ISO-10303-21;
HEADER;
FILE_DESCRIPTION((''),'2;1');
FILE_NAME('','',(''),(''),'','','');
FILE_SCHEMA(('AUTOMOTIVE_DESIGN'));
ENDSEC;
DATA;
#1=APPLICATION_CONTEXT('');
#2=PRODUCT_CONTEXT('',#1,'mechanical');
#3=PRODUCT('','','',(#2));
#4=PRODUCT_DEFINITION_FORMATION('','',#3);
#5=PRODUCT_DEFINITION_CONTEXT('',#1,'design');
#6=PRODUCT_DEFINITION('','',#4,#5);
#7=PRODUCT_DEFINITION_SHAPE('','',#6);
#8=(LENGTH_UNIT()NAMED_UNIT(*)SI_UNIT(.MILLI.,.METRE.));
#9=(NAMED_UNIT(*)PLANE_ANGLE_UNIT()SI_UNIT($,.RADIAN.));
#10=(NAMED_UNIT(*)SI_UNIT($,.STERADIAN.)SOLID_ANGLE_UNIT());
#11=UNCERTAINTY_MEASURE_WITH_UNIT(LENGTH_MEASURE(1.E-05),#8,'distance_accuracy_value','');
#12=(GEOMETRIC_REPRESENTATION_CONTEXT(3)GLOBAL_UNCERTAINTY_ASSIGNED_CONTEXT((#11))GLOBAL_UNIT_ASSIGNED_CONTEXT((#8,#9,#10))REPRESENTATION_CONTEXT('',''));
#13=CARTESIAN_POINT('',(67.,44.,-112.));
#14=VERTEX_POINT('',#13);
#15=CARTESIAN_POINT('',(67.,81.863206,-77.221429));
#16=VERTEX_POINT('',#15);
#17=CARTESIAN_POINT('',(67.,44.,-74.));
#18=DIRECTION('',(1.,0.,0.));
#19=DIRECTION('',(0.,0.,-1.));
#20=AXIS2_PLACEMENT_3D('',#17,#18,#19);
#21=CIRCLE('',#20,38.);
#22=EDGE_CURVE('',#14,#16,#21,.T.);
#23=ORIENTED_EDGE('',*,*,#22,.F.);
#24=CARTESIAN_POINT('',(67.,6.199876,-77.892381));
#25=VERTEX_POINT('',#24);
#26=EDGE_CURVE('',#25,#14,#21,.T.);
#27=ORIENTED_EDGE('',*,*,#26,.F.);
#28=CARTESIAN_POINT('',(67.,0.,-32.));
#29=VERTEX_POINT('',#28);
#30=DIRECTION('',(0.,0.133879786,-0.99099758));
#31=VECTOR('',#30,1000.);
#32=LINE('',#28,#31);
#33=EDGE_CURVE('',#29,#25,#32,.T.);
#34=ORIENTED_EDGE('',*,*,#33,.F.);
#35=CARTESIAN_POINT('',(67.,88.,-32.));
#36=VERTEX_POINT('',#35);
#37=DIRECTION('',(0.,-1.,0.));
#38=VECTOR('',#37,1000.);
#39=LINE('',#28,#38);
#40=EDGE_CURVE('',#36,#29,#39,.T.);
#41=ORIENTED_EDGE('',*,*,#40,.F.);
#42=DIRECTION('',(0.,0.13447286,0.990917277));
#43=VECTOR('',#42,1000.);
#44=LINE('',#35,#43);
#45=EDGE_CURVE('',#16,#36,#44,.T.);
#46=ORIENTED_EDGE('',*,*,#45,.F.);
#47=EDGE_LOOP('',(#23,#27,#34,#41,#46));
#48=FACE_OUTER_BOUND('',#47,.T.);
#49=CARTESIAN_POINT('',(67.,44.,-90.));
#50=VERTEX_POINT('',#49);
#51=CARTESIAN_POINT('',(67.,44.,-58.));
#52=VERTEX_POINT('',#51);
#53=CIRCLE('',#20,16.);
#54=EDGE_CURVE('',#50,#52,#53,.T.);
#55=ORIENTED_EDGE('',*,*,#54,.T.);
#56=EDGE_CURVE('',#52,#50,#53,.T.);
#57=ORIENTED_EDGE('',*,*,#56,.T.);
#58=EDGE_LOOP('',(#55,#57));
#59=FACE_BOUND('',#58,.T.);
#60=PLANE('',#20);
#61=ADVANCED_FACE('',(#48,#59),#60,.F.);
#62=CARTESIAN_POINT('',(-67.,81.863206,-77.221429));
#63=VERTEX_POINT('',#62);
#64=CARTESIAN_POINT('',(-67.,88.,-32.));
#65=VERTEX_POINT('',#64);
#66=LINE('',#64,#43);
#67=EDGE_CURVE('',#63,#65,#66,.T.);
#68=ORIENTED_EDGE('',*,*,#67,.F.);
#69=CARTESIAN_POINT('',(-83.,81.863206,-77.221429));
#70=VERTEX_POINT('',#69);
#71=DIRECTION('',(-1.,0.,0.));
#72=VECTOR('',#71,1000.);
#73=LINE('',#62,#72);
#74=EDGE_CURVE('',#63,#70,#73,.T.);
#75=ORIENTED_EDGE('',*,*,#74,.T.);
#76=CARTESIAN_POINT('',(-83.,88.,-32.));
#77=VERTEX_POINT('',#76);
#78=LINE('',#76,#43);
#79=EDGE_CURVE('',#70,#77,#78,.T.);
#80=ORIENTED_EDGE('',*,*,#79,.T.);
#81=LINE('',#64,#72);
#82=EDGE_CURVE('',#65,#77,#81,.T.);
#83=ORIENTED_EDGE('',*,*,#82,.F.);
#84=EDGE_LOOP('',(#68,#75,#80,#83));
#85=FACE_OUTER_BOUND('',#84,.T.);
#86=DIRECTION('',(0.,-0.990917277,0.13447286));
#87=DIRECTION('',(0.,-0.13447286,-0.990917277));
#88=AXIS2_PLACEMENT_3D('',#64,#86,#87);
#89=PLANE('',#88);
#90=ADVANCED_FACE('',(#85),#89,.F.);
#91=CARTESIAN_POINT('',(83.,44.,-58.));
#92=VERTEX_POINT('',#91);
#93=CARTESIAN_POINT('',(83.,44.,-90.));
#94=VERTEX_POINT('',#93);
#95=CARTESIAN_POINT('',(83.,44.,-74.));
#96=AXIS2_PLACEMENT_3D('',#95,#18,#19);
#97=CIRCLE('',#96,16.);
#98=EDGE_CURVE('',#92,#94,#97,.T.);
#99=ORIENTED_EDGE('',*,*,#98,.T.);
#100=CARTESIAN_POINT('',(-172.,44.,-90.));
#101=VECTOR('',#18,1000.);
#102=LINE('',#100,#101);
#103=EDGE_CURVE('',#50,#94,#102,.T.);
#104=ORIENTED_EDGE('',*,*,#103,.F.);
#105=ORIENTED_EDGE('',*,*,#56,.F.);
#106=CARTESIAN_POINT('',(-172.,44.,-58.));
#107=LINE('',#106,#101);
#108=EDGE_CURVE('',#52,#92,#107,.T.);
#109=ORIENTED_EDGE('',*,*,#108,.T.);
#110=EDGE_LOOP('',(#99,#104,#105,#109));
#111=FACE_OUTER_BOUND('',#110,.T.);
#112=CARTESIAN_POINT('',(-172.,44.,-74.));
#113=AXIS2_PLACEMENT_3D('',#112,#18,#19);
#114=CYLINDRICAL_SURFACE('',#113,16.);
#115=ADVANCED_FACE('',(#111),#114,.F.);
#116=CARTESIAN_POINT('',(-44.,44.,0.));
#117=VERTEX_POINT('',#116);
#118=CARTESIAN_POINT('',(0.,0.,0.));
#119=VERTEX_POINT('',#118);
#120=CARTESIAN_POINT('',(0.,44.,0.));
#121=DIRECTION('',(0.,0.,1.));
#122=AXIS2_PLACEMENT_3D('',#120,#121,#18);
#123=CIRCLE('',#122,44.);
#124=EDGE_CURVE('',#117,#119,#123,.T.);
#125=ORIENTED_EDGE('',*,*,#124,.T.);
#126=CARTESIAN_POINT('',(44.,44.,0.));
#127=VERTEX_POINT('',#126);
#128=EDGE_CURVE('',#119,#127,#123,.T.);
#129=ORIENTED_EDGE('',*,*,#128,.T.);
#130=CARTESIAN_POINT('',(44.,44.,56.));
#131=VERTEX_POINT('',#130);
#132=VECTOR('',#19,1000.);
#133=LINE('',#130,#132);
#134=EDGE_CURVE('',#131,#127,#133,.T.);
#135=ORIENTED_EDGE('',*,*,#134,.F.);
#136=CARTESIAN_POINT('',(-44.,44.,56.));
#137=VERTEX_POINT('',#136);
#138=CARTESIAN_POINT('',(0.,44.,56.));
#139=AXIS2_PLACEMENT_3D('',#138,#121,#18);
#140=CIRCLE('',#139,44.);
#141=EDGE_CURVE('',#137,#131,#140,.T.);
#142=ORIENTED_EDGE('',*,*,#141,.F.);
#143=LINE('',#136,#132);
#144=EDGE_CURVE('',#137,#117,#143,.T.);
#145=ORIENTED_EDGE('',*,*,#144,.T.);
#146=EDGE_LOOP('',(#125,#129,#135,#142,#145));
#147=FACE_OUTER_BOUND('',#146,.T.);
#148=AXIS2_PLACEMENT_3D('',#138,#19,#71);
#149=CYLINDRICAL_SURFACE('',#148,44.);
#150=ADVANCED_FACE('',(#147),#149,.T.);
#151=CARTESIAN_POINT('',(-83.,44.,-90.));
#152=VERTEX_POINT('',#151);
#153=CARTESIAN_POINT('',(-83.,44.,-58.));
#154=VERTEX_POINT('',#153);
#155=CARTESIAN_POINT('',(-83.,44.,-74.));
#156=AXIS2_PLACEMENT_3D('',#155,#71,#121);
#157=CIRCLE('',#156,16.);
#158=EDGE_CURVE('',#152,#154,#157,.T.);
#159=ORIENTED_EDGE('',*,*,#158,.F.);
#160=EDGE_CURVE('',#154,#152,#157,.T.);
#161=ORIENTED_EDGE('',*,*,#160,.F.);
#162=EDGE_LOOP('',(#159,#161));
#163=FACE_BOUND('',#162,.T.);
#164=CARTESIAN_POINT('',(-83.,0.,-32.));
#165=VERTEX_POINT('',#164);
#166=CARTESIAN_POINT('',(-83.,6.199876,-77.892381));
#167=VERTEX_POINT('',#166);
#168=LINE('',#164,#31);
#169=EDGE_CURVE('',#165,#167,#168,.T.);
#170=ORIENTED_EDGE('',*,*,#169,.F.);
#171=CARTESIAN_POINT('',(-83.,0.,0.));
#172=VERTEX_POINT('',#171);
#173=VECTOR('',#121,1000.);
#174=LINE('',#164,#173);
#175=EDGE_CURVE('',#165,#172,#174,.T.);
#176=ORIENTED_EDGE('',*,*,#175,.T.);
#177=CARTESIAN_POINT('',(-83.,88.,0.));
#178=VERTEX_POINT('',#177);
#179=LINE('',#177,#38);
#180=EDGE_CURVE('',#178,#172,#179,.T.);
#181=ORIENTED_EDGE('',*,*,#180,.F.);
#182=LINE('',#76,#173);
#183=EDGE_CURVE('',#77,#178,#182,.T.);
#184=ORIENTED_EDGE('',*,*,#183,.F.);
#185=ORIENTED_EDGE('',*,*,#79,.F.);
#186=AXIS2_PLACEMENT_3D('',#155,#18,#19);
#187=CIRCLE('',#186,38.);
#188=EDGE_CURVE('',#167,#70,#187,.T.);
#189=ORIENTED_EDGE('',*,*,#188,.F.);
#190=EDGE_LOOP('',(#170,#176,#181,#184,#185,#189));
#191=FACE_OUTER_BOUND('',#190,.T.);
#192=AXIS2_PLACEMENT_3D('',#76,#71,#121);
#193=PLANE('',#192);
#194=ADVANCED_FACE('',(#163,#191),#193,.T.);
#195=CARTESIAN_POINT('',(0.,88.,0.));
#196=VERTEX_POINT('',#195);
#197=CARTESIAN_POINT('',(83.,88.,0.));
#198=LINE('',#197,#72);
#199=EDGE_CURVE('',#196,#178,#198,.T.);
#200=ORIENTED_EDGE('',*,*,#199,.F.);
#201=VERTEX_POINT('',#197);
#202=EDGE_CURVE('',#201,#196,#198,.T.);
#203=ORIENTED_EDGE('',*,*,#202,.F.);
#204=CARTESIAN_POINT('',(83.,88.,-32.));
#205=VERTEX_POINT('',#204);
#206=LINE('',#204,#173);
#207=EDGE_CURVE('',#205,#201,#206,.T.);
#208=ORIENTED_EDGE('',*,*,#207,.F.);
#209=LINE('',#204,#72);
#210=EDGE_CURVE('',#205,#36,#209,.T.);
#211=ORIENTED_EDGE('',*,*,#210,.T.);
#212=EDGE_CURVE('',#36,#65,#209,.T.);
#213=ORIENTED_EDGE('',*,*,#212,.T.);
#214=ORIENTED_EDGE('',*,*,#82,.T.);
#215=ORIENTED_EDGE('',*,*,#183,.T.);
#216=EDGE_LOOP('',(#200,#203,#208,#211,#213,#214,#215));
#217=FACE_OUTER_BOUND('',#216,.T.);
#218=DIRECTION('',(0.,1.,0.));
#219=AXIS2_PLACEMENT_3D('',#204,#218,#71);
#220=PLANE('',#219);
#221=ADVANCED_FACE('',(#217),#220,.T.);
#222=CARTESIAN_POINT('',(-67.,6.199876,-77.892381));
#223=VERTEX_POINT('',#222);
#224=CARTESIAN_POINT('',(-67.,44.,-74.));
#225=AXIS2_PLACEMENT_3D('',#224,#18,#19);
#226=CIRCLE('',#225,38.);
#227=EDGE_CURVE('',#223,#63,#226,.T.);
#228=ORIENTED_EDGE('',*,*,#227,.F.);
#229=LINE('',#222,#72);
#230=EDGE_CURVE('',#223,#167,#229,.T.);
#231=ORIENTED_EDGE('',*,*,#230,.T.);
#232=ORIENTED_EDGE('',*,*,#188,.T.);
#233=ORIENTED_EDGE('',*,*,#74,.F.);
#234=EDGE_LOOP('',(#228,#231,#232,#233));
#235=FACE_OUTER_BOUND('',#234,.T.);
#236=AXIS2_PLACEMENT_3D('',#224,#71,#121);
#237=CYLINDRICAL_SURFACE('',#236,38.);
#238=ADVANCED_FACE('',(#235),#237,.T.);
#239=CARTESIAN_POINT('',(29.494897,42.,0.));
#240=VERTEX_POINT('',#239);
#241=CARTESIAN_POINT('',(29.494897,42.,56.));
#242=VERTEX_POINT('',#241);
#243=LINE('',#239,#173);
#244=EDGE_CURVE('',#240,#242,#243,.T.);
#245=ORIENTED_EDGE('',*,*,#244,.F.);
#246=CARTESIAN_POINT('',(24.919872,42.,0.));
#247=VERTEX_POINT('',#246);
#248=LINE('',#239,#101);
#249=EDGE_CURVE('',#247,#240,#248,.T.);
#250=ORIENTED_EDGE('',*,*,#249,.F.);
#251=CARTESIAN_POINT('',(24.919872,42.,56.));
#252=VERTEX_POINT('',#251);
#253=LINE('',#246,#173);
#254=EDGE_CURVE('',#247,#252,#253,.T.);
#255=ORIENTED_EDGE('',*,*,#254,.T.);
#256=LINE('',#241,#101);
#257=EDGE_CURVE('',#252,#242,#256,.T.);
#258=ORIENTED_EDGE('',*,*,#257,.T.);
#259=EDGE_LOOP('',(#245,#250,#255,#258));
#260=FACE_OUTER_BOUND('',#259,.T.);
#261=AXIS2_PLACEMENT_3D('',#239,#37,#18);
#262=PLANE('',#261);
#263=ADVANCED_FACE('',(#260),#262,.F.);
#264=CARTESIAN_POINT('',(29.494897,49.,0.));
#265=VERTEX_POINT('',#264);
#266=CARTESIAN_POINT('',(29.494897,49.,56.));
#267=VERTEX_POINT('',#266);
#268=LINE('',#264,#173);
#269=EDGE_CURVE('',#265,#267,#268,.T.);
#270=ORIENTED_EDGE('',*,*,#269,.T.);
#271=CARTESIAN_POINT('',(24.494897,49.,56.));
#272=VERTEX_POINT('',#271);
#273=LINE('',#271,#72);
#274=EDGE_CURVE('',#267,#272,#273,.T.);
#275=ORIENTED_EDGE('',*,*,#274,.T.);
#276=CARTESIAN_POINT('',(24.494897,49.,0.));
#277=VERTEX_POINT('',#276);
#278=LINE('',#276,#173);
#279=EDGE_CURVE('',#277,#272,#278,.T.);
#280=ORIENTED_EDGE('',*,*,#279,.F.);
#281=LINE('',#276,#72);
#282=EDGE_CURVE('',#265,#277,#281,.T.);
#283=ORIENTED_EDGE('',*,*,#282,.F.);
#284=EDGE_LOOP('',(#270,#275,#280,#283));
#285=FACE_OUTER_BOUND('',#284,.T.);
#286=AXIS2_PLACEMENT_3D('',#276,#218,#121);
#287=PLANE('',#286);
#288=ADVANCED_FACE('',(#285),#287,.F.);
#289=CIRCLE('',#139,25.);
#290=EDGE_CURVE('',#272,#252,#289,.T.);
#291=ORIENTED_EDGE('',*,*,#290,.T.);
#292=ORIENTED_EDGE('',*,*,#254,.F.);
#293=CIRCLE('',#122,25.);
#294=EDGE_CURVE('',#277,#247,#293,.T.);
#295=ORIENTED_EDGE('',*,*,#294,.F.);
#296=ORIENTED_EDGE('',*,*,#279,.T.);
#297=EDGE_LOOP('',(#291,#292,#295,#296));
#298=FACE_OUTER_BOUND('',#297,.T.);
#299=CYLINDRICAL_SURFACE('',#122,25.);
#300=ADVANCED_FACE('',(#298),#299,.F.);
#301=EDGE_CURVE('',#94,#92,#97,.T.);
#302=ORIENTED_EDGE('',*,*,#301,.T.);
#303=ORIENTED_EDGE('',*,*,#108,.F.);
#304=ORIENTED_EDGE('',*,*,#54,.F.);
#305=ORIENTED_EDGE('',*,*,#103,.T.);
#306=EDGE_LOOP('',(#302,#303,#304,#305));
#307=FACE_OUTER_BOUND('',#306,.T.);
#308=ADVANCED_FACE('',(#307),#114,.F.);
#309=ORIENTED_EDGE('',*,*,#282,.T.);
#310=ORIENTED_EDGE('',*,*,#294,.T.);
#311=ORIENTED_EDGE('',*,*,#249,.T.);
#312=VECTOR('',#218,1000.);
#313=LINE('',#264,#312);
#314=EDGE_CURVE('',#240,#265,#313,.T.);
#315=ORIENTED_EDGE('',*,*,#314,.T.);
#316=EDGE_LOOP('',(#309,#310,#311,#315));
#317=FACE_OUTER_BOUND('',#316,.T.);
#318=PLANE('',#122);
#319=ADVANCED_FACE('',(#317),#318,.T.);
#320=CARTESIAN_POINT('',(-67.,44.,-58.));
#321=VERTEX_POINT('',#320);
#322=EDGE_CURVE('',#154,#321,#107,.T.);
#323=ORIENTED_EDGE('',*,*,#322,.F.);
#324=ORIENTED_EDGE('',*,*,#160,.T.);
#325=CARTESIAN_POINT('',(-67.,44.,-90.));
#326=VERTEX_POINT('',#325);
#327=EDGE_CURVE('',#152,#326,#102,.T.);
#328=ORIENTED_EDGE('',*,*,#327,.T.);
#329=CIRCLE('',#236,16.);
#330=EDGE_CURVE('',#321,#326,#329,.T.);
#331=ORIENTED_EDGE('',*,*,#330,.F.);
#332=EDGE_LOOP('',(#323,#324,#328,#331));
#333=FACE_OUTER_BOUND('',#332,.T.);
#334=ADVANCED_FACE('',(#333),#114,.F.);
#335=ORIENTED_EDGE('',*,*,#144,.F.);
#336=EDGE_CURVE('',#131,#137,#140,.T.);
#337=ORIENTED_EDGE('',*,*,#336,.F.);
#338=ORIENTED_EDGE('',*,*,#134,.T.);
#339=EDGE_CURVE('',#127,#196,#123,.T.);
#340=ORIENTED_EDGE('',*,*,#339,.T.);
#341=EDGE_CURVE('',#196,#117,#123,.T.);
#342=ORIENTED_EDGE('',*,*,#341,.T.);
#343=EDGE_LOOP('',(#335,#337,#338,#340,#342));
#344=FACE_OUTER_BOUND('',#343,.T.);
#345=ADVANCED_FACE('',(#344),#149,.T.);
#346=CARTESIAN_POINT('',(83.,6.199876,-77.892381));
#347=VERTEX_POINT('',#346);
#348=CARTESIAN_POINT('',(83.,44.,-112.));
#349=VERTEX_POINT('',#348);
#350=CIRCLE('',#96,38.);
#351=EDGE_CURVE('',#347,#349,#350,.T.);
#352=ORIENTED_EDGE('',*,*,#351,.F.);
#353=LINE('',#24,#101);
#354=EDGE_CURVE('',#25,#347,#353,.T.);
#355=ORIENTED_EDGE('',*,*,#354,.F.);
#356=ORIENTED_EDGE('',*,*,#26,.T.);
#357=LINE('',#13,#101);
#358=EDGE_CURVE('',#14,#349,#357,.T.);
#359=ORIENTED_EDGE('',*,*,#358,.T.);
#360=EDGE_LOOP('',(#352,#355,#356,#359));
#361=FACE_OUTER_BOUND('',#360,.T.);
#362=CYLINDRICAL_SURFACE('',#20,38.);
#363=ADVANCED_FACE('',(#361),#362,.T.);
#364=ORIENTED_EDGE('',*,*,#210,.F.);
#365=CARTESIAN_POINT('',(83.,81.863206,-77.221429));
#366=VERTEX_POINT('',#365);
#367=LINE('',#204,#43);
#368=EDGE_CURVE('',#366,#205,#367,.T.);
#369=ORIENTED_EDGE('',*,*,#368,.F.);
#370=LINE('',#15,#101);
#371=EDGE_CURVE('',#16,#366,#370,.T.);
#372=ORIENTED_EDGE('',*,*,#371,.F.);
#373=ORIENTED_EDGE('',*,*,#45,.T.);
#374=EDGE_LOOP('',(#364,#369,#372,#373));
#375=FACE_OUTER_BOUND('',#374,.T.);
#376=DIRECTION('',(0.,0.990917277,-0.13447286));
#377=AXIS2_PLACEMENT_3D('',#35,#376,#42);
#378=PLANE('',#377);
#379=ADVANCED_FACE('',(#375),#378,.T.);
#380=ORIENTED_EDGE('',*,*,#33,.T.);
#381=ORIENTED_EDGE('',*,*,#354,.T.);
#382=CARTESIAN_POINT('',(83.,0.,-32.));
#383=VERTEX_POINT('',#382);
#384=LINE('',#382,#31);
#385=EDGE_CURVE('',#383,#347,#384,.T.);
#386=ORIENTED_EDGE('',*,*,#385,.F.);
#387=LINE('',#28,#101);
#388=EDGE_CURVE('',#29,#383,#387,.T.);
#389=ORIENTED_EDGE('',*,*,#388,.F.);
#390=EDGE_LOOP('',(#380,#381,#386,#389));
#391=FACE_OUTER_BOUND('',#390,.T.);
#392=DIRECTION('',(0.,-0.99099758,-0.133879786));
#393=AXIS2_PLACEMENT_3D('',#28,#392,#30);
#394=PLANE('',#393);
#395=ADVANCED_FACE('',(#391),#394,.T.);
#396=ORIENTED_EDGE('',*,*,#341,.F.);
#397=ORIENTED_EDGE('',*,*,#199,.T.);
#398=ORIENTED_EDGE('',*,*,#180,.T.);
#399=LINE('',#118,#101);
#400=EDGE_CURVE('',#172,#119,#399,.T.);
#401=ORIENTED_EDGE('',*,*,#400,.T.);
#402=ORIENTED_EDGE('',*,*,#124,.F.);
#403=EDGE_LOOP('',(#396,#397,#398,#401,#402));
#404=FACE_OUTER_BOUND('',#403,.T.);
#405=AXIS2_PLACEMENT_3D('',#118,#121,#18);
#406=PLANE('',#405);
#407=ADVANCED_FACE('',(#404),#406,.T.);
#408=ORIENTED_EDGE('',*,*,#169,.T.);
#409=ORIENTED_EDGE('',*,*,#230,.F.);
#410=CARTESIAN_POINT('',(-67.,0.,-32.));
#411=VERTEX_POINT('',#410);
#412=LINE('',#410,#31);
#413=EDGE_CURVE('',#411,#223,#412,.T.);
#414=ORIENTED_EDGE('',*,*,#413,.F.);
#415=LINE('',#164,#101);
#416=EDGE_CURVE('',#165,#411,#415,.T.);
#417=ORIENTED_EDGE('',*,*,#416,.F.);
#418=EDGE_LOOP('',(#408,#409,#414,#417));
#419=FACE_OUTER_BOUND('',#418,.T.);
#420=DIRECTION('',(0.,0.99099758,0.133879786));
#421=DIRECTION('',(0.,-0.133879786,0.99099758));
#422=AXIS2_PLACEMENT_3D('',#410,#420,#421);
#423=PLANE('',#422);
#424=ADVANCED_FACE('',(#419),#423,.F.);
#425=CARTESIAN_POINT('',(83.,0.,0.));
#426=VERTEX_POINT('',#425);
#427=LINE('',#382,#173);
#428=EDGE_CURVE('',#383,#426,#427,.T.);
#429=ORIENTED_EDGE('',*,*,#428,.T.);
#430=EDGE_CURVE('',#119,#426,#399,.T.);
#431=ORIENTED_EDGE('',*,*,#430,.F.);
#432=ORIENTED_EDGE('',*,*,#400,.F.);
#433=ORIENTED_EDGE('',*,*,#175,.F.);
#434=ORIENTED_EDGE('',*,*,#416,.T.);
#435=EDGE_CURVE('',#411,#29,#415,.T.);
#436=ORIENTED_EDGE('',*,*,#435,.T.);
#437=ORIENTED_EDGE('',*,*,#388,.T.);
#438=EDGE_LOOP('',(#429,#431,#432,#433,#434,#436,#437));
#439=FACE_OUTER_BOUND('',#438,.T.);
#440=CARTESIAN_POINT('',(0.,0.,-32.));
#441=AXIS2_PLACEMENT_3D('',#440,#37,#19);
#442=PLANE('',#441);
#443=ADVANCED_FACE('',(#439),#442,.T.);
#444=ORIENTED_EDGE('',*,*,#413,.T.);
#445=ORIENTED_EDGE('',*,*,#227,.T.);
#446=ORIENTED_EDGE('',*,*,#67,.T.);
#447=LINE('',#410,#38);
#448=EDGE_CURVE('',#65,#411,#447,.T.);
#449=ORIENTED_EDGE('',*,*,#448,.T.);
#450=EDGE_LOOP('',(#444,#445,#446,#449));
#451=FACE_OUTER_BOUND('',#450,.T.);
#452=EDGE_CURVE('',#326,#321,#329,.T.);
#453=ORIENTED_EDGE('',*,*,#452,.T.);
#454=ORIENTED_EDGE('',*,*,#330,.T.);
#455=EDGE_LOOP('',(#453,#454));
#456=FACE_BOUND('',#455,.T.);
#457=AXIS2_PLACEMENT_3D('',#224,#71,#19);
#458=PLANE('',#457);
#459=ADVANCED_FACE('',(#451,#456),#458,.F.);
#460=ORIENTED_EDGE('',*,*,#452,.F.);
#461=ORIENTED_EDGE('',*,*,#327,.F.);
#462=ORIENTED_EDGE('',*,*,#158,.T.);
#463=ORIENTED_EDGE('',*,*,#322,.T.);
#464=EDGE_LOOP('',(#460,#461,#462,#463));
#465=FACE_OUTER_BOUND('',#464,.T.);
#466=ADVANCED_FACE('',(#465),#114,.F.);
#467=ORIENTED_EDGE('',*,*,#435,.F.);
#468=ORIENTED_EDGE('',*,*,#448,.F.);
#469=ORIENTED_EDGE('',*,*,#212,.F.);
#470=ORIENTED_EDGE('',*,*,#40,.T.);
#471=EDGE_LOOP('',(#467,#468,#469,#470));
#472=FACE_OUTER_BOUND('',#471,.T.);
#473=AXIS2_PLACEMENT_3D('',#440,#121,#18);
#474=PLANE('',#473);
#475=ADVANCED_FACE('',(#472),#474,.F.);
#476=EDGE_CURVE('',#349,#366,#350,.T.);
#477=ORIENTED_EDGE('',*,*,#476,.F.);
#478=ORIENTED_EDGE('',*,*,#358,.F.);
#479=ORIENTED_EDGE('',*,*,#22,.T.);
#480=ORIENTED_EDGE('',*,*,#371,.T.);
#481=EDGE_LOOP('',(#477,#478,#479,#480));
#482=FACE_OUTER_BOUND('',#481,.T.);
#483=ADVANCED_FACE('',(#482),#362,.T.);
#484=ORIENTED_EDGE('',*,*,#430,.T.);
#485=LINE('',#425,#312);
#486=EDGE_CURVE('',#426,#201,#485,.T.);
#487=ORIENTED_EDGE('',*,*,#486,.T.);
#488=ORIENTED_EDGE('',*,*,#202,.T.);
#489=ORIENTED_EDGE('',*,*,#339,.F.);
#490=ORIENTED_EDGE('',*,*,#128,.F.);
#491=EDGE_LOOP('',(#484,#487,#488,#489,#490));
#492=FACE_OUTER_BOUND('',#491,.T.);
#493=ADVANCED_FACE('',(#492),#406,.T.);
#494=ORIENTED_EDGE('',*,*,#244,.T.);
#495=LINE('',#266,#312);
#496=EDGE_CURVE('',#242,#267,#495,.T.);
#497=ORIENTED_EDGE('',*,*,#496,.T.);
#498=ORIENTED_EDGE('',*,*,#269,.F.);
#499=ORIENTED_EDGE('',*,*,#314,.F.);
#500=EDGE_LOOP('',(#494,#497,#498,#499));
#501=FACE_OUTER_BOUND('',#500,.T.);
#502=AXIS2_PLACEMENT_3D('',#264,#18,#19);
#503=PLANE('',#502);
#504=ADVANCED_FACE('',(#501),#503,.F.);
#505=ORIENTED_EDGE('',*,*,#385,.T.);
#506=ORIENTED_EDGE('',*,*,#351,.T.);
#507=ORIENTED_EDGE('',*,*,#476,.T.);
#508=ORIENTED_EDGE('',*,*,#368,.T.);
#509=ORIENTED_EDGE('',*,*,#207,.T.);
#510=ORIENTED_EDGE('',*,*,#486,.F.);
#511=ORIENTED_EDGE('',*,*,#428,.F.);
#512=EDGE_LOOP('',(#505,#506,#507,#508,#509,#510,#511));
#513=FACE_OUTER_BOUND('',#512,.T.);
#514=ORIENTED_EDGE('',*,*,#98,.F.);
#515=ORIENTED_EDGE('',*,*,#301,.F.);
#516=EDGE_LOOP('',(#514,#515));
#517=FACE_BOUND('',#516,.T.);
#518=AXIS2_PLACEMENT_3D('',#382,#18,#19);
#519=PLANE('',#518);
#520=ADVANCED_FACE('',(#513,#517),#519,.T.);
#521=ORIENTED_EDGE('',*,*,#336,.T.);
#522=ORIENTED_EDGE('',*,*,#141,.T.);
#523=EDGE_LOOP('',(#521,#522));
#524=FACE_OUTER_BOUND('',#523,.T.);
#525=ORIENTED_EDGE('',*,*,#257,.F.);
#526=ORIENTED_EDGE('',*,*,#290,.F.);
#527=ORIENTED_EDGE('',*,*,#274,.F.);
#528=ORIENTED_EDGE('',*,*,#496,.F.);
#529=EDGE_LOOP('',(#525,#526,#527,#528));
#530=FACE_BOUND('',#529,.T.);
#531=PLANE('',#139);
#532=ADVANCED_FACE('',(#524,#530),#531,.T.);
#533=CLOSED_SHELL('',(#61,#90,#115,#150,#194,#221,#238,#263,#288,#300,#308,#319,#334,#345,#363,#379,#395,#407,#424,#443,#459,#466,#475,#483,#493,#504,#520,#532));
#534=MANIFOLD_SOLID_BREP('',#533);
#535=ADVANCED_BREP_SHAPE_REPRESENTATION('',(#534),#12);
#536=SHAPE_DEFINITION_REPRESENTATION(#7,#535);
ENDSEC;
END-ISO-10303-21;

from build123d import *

# Parameters (mm, degrees)
BASE_PLATE_DEPTH    = 32
FORK_ARM_DEPTH      = 16
HUB_SKETCH_R        = 44
HUB_88_DEPTH        = 56
KEYED_BORE_50_DEPTH = 56
PIN_HOLE_SKETCH_R   = 16
PIN_HOLES_32_DEPTH  = 255


with BuildPart() as part:
    # Base Plate Sketch → Base Plate (new body)
    with BuildSketch(Plane.XY):
        Polygon((0, 0), (83, 0), (83, 88), (-83, 88), (-83, 0), align=None)
    extrude(amount=-BASE_PLATE_DEPTH)

    # Fork Arm Sketch → Fork Arm (add)
    with BuildSketch(Plane(origin=(83, 0, 0), x_dir=(0, 0, -1), z_dir=(1, 0, 0))):
        with BuildLine():
            Line((32, 88), (77.221428654, 81.863206381))
            ThreePointArc((77.221428654, 81.863206381), (111.998506035, 44.336955652), (77.892381001, 6.199876056))
            Line((77.892381001, 6.199876056), (32, 0))
            Line((32, 0), (32, 88))
        make_face()
    fork_arm = extrude(amount=-FORK_ARM_DEPTH)

    # Fork Arm Mirror: Fork Arm across plane
    add(fork_arm.mirror(Plane(origin=(0, 0, 0), x_dir=(0, 0, 1), z_dir=(1, 0, 0))))

    # Hub Sketch → Hub Ø88 (add)
    with BuildSketch(Plane.XY):
        with Locations(Location((0, 44, 0), (0, 0, 270))):
            Circle(HUB_SKETCH_R)
    extrude(amount=HUB_88_DEPTH)

    # Keyed Bore Sketch → Keyed Bore Ø50 (cut)
    with BuildSketch(Plane.XY.offset(56)):
        with BuildLine():
            Line((24.494897428, 49), (29.494897428, 49))
            Line((29.494897428, 49), (29.494897428, 42))
            Line((29.494897428, 42), (24.919871589, 42))
            ThreePointArc((24.919871589, 42), (-24.954054766, 42.485024502), (24.494897428, 49))
        make_face()
    extrude(amount=-KEYED_BORE_50_DEPTH, mode=Mode.SUBTRACT)

    # Pin Hole Sketch → Pin Holes Ø32 (cut)
    with BuildSketch(Plane(origin=(83, 0, 0), x_dir=(0, 0, -1), z_dir=(1, 0, 0))):
        with Locations(Location((74, 44, 0), (0, 0, 180))):
            Circle(PIN_HOLE_SKETCH_R)
    extrude(amount=-PIN_HOLES_32_DEPTH, mode=Mode.SUBTRACT)


solid = part.part
